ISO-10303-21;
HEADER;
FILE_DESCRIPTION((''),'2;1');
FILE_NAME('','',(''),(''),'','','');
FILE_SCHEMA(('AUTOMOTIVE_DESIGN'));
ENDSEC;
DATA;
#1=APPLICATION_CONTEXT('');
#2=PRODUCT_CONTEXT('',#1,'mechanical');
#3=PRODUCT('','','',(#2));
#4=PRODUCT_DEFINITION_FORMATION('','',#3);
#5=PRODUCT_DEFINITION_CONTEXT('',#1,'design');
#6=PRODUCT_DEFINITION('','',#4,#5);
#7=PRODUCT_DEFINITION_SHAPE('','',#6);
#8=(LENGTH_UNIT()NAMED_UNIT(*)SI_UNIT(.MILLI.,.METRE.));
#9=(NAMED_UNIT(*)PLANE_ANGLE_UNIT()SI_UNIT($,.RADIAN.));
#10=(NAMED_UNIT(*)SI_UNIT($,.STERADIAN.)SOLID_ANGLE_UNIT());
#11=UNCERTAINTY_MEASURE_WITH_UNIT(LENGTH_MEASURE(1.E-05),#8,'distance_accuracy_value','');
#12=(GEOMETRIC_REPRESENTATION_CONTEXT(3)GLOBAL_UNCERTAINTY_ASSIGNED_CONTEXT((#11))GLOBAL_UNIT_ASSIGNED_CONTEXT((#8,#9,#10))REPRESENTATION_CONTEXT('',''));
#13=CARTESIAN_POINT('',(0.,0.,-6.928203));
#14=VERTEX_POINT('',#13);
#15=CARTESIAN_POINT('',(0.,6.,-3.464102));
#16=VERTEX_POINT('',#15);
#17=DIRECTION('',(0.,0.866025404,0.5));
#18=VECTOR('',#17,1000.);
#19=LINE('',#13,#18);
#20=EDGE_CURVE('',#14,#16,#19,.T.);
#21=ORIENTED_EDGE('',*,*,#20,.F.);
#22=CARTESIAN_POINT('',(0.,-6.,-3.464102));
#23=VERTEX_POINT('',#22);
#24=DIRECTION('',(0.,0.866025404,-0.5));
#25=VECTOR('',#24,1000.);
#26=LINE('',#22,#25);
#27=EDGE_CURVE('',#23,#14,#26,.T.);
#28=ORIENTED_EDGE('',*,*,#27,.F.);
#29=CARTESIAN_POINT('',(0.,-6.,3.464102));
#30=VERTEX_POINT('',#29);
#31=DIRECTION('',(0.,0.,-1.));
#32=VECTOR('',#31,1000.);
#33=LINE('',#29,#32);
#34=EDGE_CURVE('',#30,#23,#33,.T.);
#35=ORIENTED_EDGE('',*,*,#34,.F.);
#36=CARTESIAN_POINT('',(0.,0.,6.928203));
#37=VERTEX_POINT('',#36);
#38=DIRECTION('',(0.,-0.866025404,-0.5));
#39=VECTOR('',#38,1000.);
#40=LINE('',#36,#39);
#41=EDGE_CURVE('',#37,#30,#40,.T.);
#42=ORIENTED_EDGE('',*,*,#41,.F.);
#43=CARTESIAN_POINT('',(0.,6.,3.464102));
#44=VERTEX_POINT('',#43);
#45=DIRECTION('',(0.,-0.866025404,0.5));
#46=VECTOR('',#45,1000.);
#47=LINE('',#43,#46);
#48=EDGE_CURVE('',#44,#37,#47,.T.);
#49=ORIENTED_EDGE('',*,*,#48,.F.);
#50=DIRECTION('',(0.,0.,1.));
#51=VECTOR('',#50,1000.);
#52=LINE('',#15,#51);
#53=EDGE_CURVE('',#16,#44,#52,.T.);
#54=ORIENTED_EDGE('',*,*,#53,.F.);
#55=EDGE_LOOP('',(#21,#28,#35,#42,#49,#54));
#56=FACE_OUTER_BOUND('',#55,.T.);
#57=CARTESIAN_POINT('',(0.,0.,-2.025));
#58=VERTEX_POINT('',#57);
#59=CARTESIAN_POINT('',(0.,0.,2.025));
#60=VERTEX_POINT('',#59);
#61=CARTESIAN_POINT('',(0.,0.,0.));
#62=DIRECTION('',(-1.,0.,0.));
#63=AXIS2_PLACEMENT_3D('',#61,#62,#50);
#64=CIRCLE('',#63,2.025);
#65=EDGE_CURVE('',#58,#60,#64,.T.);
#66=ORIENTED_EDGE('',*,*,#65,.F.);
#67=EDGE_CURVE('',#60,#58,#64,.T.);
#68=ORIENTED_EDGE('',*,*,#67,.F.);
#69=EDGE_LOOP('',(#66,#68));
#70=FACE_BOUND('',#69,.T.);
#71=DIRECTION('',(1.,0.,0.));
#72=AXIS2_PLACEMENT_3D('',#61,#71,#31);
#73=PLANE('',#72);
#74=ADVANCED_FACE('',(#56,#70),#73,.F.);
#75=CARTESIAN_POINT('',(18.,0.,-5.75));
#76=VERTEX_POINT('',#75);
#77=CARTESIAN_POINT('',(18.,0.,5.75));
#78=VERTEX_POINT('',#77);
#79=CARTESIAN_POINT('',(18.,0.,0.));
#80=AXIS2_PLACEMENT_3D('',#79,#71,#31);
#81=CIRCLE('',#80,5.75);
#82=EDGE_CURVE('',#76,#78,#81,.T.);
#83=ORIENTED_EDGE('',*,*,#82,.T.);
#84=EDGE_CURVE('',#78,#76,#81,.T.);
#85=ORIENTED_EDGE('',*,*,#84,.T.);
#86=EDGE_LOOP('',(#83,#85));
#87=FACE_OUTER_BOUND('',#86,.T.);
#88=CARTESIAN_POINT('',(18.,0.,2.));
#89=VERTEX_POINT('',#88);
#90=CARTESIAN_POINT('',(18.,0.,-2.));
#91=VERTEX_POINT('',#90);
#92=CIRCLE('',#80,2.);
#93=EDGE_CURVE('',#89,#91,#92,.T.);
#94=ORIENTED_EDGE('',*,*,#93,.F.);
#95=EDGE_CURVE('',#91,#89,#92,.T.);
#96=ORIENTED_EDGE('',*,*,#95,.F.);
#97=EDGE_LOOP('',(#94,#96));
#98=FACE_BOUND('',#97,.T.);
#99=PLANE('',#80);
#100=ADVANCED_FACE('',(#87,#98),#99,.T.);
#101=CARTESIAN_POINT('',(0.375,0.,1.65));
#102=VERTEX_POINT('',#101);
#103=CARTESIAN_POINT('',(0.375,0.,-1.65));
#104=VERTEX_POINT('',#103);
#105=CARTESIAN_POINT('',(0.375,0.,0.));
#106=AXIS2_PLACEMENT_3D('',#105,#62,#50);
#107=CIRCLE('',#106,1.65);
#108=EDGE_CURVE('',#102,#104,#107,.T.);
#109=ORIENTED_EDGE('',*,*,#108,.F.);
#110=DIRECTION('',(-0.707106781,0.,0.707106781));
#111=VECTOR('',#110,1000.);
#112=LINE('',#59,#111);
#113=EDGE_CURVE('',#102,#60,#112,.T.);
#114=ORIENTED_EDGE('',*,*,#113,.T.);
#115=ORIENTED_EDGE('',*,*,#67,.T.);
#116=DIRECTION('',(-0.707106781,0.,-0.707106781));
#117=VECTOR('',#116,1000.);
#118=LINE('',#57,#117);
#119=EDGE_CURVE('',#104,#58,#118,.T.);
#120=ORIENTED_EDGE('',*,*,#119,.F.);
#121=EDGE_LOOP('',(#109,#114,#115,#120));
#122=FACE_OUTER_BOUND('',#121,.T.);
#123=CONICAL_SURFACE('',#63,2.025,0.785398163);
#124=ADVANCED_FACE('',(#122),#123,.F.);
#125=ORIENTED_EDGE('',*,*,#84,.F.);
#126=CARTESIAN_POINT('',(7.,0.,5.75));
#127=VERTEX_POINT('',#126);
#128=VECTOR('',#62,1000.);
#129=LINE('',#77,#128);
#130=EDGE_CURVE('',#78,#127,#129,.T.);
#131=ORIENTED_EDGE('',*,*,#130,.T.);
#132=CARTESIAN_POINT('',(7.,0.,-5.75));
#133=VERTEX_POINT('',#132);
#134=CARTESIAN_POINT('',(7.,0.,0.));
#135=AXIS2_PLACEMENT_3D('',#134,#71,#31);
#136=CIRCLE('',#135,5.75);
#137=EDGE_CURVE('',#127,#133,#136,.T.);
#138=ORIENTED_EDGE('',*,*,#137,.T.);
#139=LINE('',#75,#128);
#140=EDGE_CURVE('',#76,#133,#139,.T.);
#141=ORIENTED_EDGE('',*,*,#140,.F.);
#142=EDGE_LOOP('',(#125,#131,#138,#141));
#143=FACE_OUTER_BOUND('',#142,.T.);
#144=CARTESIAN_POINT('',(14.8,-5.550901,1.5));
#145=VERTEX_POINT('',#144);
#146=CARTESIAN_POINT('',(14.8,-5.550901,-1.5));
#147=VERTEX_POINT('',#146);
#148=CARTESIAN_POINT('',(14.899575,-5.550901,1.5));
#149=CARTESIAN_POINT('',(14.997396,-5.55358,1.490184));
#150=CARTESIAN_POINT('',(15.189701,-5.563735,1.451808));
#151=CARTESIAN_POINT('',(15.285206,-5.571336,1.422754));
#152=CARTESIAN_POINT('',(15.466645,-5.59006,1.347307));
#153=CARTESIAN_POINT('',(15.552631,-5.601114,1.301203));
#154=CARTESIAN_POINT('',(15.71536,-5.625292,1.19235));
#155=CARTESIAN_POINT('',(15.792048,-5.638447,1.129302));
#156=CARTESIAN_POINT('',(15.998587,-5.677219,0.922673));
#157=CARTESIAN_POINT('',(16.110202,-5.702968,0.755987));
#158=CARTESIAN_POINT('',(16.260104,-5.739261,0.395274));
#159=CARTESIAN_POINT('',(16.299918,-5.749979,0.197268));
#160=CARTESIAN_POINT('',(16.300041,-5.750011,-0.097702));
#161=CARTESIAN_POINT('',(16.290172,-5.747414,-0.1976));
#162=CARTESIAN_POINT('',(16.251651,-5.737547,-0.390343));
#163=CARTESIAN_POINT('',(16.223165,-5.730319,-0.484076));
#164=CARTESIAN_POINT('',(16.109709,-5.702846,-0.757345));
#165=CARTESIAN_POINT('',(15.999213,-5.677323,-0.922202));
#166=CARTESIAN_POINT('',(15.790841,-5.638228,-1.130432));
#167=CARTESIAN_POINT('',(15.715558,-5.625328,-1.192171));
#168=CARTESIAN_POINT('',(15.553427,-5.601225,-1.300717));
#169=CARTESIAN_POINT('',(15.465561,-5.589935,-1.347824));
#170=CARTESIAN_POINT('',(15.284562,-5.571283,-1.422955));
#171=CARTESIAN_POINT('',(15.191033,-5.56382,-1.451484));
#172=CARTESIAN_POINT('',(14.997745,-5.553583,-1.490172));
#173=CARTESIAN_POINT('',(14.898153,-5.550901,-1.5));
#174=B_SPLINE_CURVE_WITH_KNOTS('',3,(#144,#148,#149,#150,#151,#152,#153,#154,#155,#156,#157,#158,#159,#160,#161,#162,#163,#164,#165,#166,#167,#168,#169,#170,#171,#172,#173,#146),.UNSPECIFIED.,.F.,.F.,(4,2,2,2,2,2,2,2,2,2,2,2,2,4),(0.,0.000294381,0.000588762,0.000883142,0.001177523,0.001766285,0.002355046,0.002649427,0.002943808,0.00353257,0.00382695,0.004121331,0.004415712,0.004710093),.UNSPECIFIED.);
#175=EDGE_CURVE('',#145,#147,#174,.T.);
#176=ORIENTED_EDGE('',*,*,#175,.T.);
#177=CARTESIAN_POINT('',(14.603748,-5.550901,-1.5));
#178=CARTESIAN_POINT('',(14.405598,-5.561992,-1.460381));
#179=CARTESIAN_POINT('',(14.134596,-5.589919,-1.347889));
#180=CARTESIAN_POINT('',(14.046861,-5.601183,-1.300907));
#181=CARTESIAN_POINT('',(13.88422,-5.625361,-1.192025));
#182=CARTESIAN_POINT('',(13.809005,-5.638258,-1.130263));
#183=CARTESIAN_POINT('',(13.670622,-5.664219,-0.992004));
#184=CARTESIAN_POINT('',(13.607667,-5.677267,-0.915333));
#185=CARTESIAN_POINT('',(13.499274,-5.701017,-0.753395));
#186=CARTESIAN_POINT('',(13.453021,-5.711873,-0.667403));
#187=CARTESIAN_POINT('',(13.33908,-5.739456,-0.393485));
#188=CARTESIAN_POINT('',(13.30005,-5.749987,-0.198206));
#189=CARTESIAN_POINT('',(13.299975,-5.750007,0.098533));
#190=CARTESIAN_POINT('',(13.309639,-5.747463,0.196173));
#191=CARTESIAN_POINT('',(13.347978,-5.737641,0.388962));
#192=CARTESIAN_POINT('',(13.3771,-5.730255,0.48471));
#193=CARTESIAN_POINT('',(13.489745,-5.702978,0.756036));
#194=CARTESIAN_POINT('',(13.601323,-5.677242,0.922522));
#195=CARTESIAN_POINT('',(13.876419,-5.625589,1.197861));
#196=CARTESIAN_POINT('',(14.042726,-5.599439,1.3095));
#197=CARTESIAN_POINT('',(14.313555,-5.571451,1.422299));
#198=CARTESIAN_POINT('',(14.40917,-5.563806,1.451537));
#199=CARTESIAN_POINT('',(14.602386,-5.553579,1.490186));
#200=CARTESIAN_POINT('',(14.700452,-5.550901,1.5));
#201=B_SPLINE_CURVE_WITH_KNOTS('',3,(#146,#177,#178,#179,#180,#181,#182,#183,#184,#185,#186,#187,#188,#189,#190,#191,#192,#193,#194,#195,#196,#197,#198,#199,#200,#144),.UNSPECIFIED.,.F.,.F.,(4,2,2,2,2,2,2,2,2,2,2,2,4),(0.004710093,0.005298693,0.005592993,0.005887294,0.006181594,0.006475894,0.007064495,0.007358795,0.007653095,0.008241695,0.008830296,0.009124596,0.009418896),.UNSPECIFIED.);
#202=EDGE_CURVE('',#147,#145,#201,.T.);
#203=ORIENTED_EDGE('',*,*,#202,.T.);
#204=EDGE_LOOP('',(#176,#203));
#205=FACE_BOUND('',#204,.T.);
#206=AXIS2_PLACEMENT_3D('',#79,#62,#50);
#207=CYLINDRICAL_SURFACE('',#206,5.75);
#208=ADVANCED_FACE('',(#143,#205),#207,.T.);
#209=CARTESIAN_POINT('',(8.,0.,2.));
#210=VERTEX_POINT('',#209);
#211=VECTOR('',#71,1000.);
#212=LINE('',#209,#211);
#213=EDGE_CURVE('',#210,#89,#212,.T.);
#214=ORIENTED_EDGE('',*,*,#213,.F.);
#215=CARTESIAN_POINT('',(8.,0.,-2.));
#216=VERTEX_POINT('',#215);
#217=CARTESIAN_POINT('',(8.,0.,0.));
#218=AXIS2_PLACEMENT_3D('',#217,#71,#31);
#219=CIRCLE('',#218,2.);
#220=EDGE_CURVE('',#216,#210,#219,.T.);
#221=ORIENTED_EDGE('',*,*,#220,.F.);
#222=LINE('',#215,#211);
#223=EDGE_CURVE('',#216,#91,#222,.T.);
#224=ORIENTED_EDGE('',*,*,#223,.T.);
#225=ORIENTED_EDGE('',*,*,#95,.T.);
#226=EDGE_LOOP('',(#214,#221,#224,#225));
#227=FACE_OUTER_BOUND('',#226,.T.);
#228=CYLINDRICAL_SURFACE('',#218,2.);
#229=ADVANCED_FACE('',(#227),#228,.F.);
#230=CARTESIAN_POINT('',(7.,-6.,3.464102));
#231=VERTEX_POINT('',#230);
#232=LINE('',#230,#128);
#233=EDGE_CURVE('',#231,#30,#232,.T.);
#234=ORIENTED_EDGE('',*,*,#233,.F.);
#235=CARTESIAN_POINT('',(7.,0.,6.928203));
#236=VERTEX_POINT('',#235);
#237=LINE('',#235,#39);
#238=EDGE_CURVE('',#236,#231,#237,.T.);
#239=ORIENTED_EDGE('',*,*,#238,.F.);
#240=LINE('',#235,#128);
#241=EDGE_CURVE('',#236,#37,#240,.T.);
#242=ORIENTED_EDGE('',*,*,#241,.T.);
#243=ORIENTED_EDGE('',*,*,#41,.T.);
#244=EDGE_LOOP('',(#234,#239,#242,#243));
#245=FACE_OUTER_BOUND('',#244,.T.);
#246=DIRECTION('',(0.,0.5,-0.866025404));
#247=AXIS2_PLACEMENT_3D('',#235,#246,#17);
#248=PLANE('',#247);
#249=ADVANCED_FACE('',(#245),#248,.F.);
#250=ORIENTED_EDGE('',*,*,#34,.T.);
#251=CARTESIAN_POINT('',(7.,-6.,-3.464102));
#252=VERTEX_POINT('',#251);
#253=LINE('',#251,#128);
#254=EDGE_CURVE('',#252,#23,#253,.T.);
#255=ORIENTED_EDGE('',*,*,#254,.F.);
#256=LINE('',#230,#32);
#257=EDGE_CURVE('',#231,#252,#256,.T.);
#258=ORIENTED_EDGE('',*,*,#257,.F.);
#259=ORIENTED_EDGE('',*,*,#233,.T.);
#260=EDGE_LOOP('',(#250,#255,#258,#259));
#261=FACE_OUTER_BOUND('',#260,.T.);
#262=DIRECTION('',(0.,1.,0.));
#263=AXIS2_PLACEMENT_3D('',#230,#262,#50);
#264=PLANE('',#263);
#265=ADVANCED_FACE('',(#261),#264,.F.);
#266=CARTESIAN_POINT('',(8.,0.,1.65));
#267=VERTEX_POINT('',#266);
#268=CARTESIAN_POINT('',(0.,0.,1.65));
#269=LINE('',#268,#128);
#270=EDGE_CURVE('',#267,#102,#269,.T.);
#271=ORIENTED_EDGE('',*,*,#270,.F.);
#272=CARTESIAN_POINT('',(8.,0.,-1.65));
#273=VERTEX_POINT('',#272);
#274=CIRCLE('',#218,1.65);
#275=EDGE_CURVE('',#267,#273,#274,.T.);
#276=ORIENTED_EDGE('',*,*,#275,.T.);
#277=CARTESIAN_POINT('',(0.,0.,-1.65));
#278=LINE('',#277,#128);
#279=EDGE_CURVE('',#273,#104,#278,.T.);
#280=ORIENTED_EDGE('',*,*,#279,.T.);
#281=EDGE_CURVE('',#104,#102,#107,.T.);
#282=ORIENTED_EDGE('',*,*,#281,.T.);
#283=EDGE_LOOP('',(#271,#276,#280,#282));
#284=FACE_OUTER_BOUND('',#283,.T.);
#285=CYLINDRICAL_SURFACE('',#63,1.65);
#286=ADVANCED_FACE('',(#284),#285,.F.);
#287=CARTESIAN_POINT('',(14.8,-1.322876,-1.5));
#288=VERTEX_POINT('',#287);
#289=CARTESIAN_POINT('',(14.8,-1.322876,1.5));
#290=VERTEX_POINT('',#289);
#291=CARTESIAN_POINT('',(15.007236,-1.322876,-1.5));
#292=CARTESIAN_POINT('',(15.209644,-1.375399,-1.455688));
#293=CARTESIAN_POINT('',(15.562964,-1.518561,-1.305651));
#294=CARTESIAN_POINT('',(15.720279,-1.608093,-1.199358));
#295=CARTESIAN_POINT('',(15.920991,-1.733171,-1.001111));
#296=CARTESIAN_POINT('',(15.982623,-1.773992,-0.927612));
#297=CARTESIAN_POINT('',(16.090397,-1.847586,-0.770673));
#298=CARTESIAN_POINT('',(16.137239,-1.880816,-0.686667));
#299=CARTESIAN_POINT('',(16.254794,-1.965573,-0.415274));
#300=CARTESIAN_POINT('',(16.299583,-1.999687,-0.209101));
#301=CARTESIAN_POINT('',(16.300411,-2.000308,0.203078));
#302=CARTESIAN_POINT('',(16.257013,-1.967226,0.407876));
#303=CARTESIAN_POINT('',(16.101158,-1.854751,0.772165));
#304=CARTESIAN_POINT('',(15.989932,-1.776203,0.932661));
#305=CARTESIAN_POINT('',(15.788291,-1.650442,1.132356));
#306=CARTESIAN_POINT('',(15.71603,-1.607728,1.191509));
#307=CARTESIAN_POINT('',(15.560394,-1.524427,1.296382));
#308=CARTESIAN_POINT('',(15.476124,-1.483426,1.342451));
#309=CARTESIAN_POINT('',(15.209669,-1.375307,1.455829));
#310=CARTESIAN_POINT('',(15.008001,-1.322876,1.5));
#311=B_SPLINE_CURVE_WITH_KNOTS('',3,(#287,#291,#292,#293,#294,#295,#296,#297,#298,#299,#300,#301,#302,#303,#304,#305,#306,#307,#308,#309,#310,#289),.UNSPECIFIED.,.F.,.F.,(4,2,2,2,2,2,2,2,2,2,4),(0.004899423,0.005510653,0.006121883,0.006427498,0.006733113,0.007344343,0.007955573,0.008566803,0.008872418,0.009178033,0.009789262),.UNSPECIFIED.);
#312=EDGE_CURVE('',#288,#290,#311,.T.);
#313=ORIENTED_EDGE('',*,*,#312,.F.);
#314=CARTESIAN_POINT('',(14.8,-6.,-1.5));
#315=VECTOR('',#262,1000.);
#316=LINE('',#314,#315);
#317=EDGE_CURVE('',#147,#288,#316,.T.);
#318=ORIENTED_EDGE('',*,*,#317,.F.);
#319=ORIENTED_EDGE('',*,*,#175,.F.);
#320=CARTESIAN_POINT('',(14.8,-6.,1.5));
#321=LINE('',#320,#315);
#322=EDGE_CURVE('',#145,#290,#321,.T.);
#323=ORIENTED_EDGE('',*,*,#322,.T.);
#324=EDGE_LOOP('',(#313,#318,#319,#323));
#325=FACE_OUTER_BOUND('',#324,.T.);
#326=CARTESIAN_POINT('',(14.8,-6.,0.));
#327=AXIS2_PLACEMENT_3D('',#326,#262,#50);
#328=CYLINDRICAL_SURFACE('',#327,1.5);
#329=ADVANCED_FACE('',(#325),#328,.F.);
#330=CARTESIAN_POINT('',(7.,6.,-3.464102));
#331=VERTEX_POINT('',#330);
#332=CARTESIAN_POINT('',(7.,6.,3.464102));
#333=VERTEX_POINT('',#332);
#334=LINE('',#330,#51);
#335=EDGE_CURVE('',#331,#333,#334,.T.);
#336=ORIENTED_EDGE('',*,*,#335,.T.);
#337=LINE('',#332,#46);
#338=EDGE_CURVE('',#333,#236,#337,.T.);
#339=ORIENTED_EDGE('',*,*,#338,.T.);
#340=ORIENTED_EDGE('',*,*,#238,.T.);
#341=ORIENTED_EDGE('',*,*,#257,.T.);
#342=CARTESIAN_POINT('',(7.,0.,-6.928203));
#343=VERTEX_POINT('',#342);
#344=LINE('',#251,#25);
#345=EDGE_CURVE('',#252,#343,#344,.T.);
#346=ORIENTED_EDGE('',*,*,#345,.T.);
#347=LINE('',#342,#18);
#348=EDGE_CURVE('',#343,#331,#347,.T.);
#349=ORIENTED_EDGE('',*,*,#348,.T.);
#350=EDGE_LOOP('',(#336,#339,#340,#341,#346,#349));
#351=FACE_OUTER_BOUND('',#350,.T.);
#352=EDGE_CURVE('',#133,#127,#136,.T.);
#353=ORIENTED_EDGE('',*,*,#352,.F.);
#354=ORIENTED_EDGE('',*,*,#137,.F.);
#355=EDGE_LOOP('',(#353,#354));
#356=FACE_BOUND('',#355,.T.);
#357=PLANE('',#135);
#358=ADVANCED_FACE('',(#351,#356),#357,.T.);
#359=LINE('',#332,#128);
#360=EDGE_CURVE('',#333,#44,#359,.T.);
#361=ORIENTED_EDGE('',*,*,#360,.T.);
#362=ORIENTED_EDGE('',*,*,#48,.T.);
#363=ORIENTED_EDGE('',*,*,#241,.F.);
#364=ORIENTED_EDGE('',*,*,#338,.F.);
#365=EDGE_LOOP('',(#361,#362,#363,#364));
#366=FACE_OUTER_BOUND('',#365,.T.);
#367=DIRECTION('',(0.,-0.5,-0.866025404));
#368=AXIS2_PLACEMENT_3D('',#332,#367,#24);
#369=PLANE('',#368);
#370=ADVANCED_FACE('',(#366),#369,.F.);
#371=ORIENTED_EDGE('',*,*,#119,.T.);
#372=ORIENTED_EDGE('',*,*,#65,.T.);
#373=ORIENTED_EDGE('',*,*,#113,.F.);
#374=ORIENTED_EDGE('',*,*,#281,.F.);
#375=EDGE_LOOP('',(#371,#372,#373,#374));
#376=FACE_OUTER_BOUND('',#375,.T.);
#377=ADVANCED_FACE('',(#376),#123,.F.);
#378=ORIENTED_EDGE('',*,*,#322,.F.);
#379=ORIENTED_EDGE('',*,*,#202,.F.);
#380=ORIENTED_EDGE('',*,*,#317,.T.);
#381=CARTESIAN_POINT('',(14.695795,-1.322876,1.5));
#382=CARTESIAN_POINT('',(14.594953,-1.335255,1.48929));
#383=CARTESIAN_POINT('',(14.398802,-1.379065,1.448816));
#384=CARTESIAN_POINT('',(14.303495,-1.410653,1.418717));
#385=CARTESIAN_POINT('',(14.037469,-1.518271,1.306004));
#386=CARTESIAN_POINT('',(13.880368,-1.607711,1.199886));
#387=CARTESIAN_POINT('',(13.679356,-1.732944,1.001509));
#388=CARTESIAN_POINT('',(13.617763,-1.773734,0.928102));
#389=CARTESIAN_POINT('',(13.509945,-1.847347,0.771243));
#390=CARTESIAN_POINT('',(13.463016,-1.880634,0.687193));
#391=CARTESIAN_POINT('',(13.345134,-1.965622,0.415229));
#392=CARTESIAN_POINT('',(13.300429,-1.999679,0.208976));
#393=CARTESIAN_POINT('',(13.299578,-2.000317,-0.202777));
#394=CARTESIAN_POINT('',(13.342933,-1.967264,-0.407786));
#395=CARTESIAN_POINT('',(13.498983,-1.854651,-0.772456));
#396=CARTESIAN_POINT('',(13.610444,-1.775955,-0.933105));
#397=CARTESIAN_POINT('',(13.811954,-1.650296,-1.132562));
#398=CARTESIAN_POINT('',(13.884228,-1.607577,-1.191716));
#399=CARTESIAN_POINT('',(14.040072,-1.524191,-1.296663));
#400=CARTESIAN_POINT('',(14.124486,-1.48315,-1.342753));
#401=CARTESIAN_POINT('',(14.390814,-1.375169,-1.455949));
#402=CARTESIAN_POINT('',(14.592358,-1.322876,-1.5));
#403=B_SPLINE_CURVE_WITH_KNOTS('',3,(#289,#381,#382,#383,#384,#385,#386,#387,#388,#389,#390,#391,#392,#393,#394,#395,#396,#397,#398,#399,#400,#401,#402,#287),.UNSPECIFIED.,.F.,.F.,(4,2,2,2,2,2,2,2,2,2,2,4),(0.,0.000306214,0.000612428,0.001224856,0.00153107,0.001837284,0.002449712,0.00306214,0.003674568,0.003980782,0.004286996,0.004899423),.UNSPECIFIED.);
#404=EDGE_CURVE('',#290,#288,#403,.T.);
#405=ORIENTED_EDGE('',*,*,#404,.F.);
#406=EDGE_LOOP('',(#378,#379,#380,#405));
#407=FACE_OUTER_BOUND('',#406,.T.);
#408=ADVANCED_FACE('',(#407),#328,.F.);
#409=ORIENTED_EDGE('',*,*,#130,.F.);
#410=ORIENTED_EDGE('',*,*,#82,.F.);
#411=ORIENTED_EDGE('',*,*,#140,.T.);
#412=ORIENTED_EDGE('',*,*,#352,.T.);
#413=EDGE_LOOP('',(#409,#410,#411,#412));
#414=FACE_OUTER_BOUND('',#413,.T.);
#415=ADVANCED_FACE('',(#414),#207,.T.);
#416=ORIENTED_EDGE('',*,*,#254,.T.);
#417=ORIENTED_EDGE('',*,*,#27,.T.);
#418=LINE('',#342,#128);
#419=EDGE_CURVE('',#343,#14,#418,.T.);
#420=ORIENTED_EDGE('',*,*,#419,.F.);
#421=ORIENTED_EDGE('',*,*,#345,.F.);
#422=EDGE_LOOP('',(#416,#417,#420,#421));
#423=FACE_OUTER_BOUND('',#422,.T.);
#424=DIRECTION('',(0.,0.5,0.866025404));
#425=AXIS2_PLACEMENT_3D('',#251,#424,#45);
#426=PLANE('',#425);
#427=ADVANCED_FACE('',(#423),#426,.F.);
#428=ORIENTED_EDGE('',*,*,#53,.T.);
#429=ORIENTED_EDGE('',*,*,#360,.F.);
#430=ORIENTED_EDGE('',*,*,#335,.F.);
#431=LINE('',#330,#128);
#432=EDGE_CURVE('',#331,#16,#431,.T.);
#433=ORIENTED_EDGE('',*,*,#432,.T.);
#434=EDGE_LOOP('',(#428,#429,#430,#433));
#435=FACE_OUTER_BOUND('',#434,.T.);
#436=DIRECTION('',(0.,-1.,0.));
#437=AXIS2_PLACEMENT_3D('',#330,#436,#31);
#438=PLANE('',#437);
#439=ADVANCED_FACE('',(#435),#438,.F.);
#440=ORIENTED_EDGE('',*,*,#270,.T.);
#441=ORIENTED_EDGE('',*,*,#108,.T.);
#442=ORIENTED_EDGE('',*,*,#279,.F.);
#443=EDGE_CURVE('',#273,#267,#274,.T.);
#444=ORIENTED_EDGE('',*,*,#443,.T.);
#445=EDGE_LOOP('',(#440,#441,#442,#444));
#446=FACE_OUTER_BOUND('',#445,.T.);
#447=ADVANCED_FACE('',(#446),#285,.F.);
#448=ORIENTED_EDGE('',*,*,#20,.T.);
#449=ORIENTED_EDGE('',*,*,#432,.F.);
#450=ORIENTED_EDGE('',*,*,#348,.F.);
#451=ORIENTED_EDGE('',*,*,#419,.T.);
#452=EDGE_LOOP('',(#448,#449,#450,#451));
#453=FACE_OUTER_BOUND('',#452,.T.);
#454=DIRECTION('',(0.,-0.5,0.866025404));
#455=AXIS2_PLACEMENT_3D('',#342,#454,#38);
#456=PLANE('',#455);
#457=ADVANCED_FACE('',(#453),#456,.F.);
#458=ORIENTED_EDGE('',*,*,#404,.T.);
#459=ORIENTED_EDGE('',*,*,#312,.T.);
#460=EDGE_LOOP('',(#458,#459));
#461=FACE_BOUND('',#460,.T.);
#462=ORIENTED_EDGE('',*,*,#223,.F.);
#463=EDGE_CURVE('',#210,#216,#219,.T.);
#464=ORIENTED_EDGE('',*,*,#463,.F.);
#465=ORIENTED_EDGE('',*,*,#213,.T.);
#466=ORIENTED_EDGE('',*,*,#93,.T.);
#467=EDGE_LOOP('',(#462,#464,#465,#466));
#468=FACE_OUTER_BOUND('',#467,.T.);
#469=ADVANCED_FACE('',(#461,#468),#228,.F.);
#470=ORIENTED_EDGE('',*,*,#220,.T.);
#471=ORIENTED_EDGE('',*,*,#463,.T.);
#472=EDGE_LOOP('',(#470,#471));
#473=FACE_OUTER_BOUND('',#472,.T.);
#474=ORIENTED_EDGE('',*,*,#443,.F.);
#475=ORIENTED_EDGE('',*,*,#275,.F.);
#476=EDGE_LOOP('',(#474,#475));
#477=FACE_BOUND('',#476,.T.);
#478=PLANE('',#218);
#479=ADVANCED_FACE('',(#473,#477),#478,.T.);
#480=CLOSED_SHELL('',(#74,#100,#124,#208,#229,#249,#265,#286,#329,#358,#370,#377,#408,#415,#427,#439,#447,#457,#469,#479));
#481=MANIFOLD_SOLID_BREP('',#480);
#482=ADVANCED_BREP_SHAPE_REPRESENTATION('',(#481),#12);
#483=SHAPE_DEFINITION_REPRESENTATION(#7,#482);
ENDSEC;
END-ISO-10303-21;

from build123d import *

# Parameters (mm, degrees)
BOSS_EXTRUDE1_DEPTH         = 7
SKETCH2_R                   = 5.75
BOSS_EXTRUDE2_DEPTH         = 11
SKETCH3_R                   = 2
CUT_EXTRUDE1_DEPTH          = 10
M4_TAPPED_HOLE1_D           = 3.3
M4_TAPPED_HOLE1_CSINK_D     = 4.05
M4_TAPPED_HOLE1_CSINK_ANGLE = 90
SKETCH6_R                   = 1.5
CUT_EXTRUDE2_DEPTH          = 21.199009877


with BuildPart() as part:
    # Sketch1 → Boss-Extrude1 (new body)
    with BuildSketch(Plane(origin=(0, 0, 0), x_dir=(0, 0, -1), z_dir=(1, 0, 0))):
        Polygon((6.92820323, 0), (3.464101615, 6), (-3.464101615, 6), (-6.92820323, 0), (-3.464101615, -6), (3.464101615, -6), align=None)
    extrude(amount=BOSS_EXTRUDE1_DEPTH)

    # Sketch2 → Boss-Extrude2 (add)
    with BuildSketch(Plane(origin=(7, 0, 0), x_dir=(0, 0, -1), z_dir=(1, 0, 0))):
        Circle(SKETCH2_R)
    extrude(amount=BOSS_EXTRUDE2_DEPTH)

    # Sketch3 → Cut-Extrude1 (cut)
    with BuildSketch(Plane(origin=(18, 0, 0), x_dir=(0, 0, -1), z_dir=(1, 0, 0))):
        Circle(SKETCH3_R)
    extrude(amount=-CUT_EXTRUDE1_DEPTH, mode=Mode.SUBTRACT)

    # M4 Tapped Hole1 (through all)
    with Locations(Plane.ZY):
        with Locations((0, 0)):
            CounterSinkHole(M4_TAPPED_HOLE1_D / 2, M4_TAPPED_HOLE1_CSINK_D / 2, counter_sink_angle=M4_TAPPED_HOLE1_CSINK_ANGLE)

    # Sketch6 → Cut-Extrude2 (cut, through all)
    with BuildSketch(Plane(origin=(0, 0, 0), x_dir=(1, 0, 0), z_dir=(0, 1, 0))):
        with Locations(Location((14.8, 0, 0), (0, 0, 270))):
            Circle(SKETCH6_R)
    extrude(amount=-CUT_EXTRUDE2_DEPTH, mode=Mode.SUBTRACT)


solid = part.part
